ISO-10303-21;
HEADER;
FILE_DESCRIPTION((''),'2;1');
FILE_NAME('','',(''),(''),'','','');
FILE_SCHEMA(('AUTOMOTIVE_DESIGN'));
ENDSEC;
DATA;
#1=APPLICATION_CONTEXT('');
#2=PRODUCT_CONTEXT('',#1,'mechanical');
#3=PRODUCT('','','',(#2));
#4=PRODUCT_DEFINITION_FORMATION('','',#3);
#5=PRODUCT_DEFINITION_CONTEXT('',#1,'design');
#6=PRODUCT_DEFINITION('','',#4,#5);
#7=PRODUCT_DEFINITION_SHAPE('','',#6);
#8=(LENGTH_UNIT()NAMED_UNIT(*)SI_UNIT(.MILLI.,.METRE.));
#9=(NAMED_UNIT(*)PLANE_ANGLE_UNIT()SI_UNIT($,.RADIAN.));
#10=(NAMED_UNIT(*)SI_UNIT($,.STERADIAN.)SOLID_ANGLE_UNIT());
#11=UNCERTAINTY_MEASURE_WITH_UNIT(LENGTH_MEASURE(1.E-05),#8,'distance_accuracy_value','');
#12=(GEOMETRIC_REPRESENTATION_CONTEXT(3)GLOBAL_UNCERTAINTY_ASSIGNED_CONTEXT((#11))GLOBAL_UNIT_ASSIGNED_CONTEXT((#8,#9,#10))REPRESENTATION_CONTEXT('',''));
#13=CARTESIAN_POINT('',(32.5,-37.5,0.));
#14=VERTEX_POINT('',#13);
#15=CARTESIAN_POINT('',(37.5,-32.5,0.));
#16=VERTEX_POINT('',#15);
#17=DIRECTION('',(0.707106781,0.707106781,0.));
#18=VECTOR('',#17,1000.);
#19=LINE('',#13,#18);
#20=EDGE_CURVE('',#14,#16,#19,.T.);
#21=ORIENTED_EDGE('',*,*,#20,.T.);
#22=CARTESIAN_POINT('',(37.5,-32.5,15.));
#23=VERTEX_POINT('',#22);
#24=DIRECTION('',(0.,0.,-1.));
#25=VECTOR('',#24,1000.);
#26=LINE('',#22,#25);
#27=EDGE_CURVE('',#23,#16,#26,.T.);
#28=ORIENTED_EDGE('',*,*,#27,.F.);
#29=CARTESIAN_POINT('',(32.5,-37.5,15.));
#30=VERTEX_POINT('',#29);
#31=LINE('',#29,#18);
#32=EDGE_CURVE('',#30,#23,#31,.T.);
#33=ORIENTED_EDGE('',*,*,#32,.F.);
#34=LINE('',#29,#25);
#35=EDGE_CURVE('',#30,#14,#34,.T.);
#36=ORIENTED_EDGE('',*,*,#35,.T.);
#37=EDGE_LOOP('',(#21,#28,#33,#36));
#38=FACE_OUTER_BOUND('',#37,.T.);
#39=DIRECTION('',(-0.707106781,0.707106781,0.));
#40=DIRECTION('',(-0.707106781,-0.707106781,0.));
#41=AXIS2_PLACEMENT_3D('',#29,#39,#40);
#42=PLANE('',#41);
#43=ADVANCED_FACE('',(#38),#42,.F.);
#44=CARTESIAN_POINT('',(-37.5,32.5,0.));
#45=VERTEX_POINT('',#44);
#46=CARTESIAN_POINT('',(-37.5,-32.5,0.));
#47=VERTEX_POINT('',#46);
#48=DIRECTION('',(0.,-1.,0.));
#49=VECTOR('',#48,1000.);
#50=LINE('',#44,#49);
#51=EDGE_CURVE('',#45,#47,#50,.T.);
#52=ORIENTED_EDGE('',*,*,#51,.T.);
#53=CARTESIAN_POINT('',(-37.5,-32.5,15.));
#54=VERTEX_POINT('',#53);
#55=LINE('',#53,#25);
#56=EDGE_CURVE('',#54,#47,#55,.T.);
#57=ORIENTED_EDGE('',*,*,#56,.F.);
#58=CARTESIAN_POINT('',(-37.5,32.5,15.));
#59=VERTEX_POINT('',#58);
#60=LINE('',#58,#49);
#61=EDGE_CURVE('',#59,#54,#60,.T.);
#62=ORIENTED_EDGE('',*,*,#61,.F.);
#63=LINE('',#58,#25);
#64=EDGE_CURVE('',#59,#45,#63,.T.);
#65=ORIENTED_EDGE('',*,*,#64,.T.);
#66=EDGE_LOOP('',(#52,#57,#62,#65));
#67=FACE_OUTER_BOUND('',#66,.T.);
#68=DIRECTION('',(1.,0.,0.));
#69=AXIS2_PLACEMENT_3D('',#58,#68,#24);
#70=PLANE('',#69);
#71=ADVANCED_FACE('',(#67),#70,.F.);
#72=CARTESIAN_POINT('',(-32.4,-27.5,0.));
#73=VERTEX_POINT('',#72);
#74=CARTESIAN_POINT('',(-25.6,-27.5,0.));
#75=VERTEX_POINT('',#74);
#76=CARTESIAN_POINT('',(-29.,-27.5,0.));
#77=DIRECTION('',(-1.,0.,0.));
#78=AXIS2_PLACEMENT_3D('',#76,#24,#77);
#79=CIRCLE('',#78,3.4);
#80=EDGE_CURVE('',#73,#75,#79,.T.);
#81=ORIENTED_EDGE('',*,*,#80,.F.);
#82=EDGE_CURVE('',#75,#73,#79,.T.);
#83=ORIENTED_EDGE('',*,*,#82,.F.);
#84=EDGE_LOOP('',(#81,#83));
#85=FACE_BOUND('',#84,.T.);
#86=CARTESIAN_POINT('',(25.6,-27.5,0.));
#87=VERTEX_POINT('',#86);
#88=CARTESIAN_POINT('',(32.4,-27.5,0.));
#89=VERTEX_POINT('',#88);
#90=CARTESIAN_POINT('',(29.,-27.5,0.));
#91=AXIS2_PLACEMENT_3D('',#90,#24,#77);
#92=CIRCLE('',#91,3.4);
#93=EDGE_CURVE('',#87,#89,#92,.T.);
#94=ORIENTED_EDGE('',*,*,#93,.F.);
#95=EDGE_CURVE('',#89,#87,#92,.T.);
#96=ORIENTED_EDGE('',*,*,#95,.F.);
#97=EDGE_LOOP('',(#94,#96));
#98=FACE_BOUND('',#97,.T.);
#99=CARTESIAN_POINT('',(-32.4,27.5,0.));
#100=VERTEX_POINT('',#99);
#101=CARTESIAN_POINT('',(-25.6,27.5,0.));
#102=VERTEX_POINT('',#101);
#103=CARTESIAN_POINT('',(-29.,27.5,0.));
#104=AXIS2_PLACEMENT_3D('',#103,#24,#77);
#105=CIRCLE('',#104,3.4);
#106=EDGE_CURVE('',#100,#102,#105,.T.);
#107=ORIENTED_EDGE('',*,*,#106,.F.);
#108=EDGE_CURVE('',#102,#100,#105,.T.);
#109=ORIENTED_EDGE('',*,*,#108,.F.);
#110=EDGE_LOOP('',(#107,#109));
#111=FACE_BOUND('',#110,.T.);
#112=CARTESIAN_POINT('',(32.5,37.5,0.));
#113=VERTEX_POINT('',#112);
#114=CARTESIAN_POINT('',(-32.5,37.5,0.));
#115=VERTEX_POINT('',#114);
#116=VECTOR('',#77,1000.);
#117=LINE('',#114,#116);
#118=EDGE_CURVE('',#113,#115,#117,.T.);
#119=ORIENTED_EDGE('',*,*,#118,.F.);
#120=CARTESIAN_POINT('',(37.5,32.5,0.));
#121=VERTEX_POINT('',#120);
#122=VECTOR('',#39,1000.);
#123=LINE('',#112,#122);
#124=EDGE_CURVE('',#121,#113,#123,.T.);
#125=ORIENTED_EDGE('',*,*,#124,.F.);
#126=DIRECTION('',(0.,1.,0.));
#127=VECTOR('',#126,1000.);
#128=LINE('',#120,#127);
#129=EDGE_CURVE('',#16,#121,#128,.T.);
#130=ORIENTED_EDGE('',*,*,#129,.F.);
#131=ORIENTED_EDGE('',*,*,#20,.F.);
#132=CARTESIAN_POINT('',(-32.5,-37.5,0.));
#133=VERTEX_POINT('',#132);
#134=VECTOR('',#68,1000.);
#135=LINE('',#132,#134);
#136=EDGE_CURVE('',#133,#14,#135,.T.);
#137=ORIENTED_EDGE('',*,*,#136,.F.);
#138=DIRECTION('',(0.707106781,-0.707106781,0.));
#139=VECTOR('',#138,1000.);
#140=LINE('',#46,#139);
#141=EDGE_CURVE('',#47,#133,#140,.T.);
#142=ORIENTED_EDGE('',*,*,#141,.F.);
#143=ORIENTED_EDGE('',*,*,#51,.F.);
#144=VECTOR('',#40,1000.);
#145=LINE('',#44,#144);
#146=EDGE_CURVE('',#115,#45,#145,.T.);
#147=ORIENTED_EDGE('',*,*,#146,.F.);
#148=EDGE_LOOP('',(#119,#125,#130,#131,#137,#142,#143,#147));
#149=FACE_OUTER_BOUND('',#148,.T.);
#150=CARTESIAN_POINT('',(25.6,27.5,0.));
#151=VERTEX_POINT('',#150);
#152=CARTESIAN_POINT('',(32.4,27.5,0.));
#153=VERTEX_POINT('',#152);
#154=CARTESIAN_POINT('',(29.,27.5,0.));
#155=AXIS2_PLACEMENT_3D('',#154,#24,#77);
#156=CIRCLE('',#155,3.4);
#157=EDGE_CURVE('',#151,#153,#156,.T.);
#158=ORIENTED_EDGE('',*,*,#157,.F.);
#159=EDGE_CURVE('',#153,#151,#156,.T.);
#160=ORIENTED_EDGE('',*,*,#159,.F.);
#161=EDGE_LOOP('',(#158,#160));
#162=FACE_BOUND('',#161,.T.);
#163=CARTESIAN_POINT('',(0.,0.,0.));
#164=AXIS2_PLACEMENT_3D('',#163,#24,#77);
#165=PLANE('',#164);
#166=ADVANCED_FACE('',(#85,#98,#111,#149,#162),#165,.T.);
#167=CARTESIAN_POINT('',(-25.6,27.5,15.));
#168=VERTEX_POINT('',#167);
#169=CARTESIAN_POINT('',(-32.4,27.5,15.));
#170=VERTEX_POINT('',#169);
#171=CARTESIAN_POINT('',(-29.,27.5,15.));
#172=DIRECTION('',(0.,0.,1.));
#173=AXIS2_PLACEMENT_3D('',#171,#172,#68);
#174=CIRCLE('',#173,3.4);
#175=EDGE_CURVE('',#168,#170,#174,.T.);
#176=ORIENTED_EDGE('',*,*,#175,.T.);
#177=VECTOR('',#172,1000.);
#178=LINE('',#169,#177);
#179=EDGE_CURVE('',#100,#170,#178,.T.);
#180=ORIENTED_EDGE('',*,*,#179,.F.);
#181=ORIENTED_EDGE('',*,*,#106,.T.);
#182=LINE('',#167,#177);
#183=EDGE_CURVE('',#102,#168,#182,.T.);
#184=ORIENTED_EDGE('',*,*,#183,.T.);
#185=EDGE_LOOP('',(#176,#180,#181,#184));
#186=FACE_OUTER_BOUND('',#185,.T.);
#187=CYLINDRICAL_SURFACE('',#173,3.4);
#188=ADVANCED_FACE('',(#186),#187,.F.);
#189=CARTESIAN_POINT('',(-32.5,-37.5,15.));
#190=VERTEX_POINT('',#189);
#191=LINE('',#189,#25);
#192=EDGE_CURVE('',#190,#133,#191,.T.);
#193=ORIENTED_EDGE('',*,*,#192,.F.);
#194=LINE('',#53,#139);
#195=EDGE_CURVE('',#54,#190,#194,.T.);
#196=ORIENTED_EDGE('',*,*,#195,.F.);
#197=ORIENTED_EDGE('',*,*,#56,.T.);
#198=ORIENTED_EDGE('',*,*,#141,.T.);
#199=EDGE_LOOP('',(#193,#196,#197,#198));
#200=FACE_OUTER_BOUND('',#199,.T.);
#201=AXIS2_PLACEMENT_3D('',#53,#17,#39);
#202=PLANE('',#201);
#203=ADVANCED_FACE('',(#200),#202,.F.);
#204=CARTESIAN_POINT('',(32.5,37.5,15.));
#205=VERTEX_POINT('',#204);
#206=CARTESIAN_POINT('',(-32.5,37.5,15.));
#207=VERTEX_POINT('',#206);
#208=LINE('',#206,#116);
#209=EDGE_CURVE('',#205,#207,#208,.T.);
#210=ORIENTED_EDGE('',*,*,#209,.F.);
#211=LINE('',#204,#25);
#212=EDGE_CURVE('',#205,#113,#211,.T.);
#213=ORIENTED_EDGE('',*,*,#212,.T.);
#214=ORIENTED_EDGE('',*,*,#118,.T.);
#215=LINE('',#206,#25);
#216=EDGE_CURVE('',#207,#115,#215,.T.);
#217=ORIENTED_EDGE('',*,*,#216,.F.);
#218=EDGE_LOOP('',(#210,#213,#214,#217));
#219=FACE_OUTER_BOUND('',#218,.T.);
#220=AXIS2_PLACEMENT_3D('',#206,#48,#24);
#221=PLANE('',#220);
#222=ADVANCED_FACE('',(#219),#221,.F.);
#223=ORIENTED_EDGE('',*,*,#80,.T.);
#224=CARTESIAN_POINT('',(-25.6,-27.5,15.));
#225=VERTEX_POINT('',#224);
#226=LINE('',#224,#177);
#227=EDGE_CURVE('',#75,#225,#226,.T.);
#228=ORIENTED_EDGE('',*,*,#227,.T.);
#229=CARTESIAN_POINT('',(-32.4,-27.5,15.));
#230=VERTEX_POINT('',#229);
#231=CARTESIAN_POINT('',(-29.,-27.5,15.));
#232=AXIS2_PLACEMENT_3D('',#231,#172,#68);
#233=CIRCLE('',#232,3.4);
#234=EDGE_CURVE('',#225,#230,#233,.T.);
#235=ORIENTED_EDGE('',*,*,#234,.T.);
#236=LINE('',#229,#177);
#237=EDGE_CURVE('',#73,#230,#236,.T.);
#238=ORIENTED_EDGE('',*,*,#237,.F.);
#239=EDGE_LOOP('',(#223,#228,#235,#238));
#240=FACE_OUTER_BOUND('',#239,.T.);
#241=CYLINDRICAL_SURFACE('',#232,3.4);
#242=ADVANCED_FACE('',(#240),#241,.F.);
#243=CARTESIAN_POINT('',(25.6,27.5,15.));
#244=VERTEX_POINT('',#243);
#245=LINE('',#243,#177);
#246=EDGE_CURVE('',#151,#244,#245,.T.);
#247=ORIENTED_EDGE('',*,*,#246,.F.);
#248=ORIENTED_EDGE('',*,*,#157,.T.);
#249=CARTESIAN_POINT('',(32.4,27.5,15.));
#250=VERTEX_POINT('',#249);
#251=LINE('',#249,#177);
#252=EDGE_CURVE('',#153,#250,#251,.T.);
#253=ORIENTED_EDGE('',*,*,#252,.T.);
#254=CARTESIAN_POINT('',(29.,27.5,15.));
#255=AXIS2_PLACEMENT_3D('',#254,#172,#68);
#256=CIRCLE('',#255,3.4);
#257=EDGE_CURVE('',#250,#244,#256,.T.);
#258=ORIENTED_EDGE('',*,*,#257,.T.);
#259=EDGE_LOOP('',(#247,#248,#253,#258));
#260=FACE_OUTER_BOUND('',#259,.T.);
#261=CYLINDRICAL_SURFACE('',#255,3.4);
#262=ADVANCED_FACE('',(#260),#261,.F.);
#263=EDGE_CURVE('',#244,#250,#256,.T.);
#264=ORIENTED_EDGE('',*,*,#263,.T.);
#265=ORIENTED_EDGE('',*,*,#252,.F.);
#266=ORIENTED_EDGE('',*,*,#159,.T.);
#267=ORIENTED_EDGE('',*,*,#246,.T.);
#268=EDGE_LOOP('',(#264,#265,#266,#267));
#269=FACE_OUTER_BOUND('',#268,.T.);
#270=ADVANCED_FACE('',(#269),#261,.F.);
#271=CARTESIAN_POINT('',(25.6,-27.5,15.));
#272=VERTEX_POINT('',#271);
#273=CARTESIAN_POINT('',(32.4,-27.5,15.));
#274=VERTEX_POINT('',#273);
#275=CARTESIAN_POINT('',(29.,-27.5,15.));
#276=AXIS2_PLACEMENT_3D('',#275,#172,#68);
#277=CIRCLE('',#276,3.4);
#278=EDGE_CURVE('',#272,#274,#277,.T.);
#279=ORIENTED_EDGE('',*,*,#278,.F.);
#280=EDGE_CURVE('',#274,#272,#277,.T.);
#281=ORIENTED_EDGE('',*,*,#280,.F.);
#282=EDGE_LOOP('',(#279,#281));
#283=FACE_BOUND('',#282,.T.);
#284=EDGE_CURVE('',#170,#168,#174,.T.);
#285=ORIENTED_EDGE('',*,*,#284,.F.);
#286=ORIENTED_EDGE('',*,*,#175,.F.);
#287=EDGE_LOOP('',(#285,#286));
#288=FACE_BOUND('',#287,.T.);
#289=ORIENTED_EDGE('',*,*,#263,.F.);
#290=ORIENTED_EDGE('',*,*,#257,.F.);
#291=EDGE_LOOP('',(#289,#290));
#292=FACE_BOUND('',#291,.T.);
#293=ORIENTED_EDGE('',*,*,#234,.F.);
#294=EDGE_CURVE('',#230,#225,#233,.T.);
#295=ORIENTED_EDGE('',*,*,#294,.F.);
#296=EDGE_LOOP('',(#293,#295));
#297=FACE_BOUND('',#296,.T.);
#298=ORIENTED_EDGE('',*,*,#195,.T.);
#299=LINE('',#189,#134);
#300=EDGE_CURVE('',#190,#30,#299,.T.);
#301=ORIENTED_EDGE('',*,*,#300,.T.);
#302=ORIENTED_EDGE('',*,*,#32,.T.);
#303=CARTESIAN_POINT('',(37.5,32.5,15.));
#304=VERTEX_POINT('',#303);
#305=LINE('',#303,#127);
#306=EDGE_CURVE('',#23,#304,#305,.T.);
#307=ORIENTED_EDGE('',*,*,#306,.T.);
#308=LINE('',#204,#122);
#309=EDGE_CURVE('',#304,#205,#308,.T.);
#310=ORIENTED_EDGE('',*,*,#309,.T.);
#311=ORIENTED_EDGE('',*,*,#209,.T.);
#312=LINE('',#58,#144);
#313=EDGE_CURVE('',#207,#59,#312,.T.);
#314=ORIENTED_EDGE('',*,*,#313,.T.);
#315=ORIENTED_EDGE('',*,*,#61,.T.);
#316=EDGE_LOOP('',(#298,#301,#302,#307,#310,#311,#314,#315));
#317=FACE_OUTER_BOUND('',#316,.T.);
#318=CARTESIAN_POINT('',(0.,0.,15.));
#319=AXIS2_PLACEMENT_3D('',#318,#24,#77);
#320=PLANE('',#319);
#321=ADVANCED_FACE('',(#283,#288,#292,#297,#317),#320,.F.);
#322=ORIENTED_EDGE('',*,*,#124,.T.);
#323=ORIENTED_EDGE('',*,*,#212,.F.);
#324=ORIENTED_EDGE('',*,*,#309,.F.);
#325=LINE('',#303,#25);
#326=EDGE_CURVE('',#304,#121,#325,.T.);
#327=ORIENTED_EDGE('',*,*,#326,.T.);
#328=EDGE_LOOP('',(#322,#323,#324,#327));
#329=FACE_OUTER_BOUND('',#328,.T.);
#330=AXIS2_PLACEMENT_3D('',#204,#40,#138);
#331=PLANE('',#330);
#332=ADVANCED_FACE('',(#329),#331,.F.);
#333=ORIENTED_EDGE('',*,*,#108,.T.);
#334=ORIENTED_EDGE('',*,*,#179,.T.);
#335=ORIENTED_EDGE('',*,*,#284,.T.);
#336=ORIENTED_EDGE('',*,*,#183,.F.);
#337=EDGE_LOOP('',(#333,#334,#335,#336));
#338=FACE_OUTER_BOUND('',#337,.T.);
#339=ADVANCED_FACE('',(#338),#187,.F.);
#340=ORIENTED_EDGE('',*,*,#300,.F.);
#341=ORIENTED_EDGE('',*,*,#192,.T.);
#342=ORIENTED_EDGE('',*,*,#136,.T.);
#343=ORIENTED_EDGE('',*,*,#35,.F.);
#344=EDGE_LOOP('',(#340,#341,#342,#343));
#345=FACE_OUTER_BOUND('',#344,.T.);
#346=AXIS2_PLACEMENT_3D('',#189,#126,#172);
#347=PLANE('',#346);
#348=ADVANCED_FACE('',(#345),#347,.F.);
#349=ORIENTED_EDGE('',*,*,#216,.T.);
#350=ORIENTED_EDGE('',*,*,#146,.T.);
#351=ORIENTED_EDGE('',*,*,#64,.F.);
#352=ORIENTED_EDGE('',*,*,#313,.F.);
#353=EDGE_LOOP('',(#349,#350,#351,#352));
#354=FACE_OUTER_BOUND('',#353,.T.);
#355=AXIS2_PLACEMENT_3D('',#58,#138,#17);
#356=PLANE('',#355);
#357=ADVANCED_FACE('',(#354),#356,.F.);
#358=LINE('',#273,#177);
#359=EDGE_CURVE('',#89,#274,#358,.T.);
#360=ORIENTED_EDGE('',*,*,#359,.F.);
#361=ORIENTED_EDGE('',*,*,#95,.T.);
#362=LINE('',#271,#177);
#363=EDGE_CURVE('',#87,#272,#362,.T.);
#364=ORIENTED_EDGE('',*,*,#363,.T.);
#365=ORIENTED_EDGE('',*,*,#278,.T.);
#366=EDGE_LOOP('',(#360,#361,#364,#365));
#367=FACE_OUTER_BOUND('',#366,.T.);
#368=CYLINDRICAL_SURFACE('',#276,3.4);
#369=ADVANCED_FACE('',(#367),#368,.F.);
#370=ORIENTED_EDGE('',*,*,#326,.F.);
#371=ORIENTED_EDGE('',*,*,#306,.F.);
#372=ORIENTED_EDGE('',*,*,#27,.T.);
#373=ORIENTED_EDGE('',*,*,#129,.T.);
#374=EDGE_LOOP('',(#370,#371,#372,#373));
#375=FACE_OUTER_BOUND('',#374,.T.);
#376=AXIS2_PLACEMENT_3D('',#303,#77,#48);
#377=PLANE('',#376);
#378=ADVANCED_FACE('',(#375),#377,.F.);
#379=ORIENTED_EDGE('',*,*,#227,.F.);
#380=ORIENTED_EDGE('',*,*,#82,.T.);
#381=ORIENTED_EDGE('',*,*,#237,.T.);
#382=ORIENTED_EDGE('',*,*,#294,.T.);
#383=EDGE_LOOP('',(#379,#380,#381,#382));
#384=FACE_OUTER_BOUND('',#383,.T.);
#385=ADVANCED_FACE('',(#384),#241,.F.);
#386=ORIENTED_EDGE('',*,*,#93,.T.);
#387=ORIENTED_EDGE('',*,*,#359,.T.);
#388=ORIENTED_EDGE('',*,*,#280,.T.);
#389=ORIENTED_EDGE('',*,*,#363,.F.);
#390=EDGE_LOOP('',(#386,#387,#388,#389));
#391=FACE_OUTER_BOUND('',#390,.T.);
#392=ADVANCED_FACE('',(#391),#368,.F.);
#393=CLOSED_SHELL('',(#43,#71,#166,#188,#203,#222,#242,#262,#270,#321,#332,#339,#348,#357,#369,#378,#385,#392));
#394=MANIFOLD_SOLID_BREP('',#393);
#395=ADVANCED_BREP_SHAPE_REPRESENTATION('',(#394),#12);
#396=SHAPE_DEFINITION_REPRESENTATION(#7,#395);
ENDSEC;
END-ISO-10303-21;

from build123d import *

# Parameters (mm, degrees)
BOSS_EXTRUDE1_DEPTH   = 15
M8_TAPPED_HOLE1_D     = 6.8
M8_TAPPED_HOLE1_DEPTH = 19.75
M8_TAPPED_HOLE1_TIP   = 2.042926105


with BuildPart() as part:
    # Sketch1 → Boss-Extrude1 (new body)
    with BuildSketch(Plane.XY):
        Polygon((-37.5, 32.5), (-32.5, 37.5), (32.5, 37.5), (37.5, 32.5), (37.5, -32.5), (32.5, -37.5), (-32.5, -37.5), (-37.5, -32.5), align=None)
    extrude(amount=BOSS_EXTRUDE1_DEPTH)

    # M8 Tapped Hole1
    with Locations(Plane.XY.offset(15)):
        with Locations((-29, 27.5), (29, 27.5), (29, -27.5), (-29, -27.5)):
            Hole(M8_TAPPED_HOLE1_D / 2, depth=M8_TAPPED_HOLE1_DEPTH)
            with Locations((0, 0, -(M8_TAPPED_HOLE1_DEPTH + M8_TAPPED_HOLE1_TIP / 2))):  # 118° drill point
                Cone(0, M8_TAPPED_HOLE1_D / 2, M8_TAPPED_HOLE1_TIP, mode=Mode.SUBTRACT)


solid = part.part
